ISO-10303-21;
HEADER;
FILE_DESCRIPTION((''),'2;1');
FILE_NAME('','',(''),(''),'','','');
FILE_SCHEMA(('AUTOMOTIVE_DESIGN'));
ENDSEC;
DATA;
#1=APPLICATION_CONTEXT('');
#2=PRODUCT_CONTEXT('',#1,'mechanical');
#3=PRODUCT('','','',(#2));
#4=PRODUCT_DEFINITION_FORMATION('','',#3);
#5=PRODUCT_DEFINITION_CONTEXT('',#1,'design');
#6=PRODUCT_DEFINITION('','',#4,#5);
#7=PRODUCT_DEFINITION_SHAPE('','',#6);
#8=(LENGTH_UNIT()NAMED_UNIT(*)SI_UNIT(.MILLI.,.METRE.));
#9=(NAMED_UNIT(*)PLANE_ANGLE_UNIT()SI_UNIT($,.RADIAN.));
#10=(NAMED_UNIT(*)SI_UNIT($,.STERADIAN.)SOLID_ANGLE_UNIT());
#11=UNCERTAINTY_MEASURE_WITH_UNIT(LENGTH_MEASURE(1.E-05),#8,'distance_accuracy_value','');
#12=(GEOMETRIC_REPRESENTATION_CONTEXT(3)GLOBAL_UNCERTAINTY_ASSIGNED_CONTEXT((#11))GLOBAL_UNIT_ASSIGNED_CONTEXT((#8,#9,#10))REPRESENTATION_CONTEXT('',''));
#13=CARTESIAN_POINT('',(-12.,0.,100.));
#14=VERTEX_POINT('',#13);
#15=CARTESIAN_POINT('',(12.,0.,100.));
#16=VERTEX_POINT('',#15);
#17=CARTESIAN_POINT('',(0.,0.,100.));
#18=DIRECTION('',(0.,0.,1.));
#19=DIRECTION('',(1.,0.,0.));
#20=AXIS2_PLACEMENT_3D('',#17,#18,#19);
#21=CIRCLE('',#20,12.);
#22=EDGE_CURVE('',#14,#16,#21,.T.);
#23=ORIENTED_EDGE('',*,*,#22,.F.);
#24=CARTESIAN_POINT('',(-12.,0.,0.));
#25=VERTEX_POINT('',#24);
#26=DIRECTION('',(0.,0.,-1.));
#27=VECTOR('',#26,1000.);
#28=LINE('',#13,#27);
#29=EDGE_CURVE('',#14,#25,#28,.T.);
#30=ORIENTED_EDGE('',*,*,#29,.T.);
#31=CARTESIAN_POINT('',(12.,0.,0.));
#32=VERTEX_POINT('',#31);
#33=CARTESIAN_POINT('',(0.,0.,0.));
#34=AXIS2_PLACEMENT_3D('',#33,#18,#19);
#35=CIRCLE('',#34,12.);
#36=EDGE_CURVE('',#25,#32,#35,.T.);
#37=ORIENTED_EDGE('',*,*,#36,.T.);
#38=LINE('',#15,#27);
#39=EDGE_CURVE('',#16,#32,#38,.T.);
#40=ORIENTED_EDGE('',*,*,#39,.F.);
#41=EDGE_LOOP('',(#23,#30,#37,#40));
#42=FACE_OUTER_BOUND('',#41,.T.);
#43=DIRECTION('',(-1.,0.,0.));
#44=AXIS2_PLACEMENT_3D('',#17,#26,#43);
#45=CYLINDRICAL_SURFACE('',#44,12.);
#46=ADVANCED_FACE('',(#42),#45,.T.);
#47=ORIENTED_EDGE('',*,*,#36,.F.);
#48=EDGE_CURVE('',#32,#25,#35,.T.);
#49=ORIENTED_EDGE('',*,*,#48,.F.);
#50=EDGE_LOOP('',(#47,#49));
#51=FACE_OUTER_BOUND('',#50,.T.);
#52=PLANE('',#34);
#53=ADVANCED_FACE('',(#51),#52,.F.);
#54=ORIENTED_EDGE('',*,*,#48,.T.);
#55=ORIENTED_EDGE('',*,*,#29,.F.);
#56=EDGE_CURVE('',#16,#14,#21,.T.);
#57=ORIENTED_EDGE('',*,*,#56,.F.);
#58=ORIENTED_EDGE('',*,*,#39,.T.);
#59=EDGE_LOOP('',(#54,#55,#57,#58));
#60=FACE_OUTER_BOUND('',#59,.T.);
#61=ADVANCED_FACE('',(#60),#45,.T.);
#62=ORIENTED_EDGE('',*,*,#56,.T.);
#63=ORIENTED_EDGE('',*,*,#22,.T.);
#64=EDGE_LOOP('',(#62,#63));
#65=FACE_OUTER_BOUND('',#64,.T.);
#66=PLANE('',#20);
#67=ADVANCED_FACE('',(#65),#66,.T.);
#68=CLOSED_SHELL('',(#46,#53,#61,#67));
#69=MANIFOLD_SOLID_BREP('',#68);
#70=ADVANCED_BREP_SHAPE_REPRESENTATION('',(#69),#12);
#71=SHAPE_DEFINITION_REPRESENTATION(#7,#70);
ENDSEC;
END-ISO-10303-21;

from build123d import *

# Parameters (mm, degrees)
SKETCH1_R           = 12
BOSS_EXTRUDE1_DEPTH = 100


with BuildPart() as part:
    # Sketch1 → Boss-Extrude1 (new body)
    with BuildSketch(Plane.XY):
        Circle(SKETCH1_R)
    extrude(amount=BOSS_EXTRUDE1_DEPTH)


solid = part.part
